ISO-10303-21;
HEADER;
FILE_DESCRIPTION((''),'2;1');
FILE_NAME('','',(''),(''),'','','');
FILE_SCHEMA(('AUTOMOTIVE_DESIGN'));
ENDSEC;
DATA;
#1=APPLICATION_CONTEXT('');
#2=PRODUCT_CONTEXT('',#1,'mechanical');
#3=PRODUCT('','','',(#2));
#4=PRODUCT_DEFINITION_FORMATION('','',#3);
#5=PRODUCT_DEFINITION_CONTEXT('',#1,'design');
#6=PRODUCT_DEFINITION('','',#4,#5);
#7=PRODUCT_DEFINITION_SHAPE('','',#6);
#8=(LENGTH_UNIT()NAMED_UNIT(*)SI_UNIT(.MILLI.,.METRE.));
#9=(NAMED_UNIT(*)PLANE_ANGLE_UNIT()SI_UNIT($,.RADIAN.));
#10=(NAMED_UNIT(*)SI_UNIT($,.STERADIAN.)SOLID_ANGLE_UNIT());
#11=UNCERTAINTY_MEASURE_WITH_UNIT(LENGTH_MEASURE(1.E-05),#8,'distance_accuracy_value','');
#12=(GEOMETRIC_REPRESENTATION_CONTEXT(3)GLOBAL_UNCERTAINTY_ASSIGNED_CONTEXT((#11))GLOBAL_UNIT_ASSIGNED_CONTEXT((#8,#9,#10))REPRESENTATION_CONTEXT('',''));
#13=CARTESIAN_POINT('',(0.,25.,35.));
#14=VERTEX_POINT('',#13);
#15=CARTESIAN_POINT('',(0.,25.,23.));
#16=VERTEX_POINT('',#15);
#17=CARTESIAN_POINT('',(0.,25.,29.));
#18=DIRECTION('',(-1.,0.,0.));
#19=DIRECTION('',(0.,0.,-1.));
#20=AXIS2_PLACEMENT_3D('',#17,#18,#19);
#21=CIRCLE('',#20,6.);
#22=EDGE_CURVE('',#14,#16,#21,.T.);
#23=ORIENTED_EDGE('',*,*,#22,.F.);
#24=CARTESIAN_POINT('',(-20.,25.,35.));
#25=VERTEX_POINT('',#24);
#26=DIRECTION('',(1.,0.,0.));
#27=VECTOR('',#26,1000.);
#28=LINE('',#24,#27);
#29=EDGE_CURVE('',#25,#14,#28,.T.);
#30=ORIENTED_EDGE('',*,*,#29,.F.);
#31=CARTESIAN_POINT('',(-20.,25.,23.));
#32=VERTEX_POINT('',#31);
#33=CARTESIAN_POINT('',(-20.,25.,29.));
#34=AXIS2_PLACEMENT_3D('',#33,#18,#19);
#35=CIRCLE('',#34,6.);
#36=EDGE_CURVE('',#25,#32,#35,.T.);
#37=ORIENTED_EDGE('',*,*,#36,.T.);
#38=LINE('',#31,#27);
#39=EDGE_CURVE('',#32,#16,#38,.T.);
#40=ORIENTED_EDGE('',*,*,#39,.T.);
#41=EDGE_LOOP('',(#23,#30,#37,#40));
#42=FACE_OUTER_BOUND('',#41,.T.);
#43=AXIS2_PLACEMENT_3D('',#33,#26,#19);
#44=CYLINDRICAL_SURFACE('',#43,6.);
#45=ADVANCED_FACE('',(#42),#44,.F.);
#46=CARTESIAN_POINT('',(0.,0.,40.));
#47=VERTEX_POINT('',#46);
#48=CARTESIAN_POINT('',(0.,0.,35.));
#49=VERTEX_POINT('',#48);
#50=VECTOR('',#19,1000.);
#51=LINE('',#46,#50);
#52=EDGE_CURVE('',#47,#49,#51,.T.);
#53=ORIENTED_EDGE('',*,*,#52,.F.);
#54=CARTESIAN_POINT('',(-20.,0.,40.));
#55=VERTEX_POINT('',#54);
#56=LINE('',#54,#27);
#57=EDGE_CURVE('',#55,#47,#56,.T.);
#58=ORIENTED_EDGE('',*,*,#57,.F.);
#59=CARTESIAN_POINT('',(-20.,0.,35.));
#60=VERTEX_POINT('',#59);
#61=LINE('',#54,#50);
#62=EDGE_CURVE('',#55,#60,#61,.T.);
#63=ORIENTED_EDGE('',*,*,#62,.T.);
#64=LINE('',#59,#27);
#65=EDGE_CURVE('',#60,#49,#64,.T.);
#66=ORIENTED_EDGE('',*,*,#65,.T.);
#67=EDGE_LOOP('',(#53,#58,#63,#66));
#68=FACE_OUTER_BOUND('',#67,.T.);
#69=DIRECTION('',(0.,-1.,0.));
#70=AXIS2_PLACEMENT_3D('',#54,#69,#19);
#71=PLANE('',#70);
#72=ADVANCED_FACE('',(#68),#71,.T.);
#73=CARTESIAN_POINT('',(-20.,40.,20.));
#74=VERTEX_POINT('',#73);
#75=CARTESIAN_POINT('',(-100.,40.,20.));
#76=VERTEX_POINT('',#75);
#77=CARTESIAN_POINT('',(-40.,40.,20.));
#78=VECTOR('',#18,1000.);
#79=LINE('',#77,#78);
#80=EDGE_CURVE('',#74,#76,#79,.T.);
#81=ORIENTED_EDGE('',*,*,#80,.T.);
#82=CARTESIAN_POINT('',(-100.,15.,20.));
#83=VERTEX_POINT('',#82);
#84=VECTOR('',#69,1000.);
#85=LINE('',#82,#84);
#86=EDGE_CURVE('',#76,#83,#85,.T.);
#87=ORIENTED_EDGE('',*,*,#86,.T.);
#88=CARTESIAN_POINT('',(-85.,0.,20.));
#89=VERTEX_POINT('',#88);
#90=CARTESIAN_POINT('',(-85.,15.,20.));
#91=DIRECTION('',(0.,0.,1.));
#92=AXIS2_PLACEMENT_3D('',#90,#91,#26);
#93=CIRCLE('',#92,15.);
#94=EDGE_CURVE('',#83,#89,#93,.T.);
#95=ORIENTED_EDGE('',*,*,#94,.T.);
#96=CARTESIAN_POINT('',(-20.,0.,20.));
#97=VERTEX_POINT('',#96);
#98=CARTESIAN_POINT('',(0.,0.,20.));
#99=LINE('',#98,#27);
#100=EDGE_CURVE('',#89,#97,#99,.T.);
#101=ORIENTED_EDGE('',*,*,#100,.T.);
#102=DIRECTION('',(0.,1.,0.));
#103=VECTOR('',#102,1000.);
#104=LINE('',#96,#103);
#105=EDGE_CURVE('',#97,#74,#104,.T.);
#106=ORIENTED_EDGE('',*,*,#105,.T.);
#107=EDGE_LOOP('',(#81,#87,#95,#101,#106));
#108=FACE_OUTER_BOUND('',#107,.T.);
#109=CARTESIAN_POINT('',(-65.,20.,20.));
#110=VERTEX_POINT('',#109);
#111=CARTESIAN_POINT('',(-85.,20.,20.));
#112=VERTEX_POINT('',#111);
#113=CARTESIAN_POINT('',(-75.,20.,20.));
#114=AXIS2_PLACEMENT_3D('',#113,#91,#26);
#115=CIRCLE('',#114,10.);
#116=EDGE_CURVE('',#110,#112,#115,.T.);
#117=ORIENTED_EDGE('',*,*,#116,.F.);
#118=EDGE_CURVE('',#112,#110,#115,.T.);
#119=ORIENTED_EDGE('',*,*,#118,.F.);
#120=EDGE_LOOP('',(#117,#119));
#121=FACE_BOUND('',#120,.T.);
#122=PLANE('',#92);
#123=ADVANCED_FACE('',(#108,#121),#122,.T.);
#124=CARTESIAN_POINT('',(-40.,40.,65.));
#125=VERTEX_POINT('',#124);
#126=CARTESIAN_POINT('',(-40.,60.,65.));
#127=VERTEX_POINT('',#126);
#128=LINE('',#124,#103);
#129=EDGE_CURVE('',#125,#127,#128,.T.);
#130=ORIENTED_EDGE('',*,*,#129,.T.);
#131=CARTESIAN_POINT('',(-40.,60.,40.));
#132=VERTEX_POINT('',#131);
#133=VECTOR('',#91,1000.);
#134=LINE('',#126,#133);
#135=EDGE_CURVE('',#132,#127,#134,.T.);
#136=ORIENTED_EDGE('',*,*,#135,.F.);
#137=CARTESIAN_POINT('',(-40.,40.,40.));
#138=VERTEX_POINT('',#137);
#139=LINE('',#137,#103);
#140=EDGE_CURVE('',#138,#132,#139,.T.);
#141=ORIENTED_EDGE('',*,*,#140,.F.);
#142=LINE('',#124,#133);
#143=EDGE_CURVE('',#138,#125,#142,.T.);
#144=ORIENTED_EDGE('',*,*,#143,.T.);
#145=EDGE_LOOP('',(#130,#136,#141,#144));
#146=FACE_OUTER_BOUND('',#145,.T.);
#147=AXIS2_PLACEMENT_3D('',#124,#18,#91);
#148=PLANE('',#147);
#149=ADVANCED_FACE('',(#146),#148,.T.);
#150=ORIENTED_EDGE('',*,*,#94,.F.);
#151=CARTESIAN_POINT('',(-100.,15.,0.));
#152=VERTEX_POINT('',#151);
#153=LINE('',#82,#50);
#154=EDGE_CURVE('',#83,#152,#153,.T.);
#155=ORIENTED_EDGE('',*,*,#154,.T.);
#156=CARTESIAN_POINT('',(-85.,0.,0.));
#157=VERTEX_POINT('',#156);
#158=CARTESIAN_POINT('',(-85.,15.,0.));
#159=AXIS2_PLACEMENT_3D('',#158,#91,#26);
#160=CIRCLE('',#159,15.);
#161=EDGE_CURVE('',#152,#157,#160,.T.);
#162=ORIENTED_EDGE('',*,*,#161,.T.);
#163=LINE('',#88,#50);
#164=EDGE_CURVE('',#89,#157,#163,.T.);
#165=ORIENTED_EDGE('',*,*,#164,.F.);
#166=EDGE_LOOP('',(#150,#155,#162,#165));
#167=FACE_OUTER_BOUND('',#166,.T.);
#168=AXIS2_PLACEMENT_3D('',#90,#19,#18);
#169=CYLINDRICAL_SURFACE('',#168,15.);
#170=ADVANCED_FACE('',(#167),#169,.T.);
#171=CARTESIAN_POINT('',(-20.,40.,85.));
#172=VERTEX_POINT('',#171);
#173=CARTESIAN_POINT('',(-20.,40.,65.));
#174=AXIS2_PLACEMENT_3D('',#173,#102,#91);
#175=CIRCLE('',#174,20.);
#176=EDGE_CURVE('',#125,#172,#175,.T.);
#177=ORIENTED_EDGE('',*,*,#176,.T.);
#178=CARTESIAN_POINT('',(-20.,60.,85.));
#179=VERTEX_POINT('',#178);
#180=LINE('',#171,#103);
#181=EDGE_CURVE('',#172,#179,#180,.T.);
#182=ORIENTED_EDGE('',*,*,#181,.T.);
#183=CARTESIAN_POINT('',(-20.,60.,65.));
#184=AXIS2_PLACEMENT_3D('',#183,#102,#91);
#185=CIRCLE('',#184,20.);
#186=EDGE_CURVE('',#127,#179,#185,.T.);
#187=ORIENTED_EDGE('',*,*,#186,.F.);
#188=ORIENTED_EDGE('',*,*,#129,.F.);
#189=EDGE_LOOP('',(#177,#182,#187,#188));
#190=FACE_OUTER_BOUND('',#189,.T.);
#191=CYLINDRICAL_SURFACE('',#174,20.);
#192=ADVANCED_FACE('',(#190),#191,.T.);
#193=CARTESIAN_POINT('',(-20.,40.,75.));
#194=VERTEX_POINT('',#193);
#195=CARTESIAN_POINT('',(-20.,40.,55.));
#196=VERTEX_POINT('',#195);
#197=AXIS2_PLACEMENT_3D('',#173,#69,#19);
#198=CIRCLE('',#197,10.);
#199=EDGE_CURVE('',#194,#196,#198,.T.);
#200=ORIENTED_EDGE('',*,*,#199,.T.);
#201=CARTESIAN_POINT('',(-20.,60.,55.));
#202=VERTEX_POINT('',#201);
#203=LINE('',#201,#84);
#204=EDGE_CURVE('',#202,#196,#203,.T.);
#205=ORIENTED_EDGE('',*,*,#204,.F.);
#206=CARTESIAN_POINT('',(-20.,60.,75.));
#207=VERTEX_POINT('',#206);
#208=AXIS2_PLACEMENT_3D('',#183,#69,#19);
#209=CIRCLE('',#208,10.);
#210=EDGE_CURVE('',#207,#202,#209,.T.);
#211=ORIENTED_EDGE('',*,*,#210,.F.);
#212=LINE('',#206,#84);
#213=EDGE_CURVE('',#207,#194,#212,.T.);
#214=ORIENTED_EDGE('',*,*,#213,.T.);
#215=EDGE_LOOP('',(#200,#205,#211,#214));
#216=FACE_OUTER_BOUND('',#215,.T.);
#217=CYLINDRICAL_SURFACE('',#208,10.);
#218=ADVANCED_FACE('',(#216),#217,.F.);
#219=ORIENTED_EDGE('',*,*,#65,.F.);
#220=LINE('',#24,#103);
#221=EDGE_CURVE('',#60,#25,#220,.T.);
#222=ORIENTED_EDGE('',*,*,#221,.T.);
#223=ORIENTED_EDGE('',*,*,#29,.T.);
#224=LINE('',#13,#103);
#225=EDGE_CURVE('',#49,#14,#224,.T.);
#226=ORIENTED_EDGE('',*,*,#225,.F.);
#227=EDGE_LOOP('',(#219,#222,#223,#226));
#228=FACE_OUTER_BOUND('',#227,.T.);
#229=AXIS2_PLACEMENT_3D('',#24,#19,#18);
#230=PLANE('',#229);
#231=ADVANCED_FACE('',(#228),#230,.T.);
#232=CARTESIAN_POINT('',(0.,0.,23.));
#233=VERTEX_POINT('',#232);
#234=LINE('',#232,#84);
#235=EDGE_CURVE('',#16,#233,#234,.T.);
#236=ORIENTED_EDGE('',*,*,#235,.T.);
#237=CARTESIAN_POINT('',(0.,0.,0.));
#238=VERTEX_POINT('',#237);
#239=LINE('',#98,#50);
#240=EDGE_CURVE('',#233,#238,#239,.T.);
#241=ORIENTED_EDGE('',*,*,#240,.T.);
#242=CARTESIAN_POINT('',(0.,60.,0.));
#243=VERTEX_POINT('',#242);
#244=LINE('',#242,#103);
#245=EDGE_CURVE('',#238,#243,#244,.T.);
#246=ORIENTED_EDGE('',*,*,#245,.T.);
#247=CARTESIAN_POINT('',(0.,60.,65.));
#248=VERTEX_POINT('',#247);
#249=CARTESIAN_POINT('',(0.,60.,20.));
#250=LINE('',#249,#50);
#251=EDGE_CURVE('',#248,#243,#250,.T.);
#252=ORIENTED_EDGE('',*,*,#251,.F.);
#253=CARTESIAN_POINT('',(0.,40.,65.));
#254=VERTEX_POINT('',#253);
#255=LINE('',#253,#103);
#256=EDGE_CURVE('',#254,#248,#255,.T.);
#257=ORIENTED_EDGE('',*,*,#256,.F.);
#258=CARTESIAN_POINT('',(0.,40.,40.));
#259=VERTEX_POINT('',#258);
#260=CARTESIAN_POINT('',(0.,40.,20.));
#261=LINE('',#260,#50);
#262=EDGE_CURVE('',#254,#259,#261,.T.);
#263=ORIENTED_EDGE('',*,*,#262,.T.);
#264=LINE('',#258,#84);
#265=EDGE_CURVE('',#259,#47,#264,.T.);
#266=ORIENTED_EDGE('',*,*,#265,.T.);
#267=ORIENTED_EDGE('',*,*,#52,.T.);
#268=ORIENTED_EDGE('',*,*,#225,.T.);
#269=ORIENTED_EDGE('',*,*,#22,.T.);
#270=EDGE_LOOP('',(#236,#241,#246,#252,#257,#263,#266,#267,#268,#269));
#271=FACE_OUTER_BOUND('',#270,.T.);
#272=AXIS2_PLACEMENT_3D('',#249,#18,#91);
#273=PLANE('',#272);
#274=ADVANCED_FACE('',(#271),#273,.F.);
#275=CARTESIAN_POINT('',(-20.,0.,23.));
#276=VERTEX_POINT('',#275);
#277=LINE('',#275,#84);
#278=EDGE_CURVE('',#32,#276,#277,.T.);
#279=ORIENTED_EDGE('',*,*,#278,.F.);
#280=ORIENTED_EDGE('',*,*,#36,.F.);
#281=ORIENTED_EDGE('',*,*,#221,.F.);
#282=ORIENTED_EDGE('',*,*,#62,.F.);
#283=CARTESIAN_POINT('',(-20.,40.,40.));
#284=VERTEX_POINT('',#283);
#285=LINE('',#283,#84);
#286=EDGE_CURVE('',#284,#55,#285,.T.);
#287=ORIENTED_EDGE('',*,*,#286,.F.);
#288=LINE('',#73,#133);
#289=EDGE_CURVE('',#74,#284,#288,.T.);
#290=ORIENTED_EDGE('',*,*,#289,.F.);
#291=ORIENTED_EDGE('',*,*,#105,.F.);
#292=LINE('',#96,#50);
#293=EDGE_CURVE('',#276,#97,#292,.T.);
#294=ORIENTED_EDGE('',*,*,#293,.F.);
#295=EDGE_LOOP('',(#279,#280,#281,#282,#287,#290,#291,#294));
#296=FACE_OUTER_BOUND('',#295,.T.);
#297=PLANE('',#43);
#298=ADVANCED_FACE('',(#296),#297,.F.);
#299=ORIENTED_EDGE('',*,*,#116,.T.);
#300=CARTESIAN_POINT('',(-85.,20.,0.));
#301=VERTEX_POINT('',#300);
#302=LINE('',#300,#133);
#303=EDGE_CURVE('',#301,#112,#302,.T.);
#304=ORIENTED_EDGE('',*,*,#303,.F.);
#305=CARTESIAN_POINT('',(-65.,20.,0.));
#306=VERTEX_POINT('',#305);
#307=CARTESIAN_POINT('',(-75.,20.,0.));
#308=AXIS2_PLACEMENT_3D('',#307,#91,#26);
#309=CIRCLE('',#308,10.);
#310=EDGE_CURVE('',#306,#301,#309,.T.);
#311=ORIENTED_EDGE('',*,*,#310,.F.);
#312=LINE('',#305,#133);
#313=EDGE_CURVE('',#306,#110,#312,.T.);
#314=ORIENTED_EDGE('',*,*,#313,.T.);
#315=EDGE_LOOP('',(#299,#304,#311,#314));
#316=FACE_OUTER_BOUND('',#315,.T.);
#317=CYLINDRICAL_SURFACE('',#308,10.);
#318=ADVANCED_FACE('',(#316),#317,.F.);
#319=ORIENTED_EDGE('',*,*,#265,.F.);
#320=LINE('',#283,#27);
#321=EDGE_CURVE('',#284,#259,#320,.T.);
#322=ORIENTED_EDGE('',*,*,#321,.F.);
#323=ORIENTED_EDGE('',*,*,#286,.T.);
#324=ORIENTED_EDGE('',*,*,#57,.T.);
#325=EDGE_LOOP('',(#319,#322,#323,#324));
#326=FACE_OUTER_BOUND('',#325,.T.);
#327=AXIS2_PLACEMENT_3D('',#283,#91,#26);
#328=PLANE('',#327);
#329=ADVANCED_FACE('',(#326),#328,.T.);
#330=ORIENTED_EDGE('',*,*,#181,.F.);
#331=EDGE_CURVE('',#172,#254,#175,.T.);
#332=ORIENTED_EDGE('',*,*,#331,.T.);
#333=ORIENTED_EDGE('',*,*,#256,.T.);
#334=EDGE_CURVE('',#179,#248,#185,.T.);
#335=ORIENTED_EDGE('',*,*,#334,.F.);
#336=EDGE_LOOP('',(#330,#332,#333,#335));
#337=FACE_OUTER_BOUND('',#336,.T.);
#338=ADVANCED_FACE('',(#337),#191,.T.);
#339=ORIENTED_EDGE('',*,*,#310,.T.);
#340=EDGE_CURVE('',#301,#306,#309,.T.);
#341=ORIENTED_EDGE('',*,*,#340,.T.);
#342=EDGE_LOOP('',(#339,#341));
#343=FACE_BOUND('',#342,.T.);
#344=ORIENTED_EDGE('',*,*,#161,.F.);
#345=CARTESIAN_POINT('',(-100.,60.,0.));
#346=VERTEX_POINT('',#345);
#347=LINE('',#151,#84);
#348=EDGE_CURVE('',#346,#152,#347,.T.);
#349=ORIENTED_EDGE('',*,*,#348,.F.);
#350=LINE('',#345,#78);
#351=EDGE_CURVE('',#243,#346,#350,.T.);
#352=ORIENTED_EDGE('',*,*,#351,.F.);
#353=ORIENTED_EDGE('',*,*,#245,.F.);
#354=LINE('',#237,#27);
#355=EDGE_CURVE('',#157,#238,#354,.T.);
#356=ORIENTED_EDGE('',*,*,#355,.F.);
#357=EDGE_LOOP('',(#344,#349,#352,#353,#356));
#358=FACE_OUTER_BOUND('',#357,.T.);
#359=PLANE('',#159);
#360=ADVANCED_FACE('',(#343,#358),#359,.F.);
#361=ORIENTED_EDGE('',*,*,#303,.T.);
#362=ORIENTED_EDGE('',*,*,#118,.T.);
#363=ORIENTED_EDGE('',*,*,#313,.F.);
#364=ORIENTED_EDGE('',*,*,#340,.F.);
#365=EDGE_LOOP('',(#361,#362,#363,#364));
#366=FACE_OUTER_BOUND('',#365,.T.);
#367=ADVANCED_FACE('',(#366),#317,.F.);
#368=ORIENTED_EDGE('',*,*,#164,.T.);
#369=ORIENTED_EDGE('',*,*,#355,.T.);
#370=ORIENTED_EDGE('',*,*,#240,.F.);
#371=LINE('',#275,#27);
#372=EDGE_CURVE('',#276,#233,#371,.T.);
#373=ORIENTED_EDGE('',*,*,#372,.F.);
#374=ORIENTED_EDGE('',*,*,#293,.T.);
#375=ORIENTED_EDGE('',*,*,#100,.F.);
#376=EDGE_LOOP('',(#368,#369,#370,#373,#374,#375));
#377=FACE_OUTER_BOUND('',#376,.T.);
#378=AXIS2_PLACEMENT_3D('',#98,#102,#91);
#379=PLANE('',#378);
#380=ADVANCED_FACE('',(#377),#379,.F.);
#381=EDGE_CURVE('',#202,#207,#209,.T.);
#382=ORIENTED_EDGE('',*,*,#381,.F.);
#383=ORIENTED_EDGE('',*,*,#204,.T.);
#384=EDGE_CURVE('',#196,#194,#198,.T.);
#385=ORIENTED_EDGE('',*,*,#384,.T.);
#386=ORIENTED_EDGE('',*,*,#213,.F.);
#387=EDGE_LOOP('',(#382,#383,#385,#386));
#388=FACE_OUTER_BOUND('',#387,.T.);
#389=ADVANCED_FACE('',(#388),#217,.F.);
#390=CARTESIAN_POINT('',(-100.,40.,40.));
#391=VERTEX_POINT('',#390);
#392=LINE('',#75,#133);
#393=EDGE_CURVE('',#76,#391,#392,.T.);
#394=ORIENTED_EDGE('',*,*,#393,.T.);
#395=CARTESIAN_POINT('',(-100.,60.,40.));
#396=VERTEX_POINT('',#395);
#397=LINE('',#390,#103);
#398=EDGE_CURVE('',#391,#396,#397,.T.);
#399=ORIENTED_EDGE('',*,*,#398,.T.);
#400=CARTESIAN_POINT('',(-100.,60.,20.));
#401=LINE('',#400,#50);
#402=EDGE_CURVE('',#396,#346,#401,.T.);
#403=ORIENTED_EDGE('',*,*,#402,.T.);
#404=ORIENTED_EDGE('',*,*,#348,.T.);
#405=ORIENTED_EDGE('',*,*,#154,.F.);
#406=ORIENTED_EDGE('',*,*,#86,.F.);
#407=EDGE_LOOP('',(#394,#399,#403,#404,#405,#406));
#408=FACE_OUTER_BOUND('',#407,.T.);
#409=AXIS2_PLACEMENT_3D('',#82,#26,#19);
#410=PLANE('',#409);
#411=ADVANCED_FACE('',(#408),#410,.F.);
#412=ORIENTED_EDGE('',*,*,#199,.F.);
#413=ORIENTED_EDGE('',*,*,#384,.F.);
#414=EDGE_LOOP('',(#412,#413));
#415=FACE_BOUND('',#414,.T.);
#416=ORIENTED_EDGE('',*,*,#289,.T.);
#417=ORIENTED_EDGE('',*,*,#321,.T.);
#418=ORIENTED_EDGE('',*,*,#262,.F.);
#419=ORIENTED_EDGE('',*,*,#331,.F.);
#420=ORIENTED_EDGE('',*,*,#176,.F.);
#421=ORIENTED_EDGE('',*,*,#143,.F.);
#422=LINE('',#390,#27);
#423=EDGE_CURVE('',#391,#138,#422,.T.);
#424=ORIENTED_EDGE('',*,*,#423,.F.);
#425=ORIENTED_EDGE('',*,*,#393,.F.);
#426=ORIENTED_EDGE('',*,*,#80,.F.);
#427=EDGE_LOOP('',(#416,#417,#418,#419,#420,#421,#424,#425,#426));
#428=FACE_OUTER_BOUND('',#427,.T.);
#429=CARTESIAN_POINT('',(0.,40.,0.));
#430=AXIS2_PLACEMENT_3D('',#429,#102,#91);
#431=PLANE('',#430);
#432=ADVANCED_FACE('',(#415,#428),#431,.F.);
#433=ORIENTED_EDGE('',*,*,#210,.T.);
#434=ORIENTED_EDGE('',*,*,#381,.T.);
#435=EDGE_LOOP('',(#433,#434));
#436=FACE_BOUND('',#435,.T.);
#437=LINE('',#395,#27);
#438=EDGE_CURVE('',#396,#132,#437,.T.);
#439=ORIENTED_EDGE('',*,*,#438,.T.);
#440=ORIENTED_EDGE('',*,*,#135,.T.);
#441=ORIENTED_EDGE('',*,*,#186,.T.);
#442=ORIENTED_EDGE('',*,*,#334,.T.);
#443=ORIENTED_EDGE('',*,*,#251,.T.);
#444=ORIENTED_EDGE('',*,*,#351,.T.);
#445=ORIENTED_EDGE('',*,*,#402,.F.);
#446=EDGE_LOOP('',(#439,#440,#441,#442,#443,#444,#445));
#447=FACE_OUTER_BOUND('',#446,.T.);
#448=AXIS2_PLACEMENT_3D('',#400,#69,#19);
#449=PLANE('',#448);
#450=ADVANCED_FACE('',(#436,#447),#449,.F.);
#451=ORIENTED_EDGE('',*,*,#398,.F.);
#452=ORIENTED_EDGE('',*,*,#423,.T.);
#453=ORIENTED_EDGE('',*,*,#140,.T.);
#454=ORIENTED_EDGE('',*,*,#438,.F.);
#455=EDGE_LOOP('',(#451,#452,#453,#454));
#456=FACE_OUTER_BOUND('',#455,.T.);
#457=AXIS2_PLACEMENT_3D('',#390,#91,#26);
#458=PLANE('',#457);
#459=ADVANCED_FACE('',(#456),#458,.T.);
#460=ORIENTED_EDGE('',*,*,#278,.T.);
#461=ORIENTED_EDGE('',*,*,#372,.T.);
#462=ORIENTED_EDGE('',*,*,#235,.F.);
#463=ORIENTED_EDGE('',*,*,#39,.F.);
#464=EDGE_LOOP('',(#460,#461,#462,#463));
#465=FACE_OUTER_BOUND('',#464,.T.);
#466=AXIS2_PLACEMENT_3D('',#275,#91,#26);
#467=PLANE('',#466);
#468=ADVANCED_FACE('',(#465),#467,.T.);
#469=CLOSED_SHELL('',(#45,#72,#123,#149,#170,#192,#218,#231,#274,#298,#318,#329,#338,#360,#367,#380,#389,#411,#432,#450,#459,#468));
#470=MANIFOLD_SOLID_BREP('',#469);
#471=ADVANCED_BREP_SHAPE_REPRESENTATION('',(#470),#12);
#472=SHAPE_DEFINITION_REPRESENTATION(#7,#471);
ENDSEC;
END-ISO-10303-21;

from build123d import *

# Parameters (mm, degrees)
BASE_BLOCK_DEPTH   = 20
HUB_BOSS_DEPTH     = 20
LEG_PROFILE_W      = 60
LEG_PROFILE_H      = 20
LEG_DEPTH          = 20
TOP_ARM_DEPTH      = 20
HUB_BORE_SKETCH_R  = 10
HUB_BORE_CUT_DEPTH = 20
LEG_SLOT_SKETCH_R  = 10
LEG_SLOT_CUT_DEPTH = 20


with BuildPart() as part:
    # Base Block Profile → Base Block (new body)
    with BuildSketch(Plane.XY):
        with BuildLine():
            Line((0, 0), (-85, 0))
            ThreePointArc((-85, 0), (-95.606601718, 4.393398282), (-100, 15))
            Line((-100, 15), (-100, 60))
            Line((-100, 60), (0, 60))
            Line((0, 60), (0, 0))
        make_face()
    extrude(amount=BASE_BLOCK_DEPTH)

    # Hub Boss Profile → Hub Boss (add)
    with BuildSketch(Plane(origin=(0, 0, 0), x_dir=(0, 0, -1), z_dir=(1, 0, 0))):
        with BuildLine():
            Line((-20, 0), (-20, 40))
            Line((-20, 40), (-40, 40))
            Line((-40, 40), (-40, 0))
            Line((-40, 0), (-35, 0))
            Line((-35, 0), (-35, 25))
            ThreePointArc((-35, 25), (-29, 31), (-23, 25))
            Line((-23, 25), (-23, 0))
            Line((-23, 0), (-20, 0))
        make_face()
    extrude(amount=-HUB_BOSS_DEPTH)

    # Leg Profile → Leg (add)
    with BuildSketch(Plane(origin=(0, 60, 0), x_dir=(1, 0, 0), z_dir=(0, 1, 0))):
        with Locations((-70, -30)):
            Rectangle(LEG_PROFILE_W, LEG_PROFILE_H)
    extrude(amount=-LEG_DEPTH)

    # Top Arm Profile → Top Arm (add)
    with BuildSketch(Plane(origin=(0, 60, 0), x_dir=(1, 0, 0), z_dir=(0, 1, 0))):
        with BuildLine():
            Line((-40, -20), (0, -20))
            Line((0, -20), (0, -65))
            ThreePointArc((0, -65), (-20, -85), (-40, -65))
            Line((-40, -65), (-40, -20))
        make_face()
    extrude(amount=-TOP_ARM_DEPTH)

    # Hub Bore Sketch → Hub Bore Cut (cut)
    with BuildSketch(Plane.XZ.offset(-40)):
        with Locations(Location((-20, 65, 0), (0, 0, 270))):
            Circle(HUB_BORE_SKETCH_R)
    extrude(amount=-HUB_BORE_CUT_DEPTH, mode=Mode.SUBTRACT)

    # Leg Slot Sketch → Leg Slot Cut (cut)
    with BuildSketch(Plane.XY.offset(20)):
        with Locations((-75, 20)):
            Circle(LEG_SLOT_SKETCH_R)
    extrude(amount=-LEG_SLOT_CUT_DEPTH, mode=Mode.SUBTRACT)


solid = part.part
